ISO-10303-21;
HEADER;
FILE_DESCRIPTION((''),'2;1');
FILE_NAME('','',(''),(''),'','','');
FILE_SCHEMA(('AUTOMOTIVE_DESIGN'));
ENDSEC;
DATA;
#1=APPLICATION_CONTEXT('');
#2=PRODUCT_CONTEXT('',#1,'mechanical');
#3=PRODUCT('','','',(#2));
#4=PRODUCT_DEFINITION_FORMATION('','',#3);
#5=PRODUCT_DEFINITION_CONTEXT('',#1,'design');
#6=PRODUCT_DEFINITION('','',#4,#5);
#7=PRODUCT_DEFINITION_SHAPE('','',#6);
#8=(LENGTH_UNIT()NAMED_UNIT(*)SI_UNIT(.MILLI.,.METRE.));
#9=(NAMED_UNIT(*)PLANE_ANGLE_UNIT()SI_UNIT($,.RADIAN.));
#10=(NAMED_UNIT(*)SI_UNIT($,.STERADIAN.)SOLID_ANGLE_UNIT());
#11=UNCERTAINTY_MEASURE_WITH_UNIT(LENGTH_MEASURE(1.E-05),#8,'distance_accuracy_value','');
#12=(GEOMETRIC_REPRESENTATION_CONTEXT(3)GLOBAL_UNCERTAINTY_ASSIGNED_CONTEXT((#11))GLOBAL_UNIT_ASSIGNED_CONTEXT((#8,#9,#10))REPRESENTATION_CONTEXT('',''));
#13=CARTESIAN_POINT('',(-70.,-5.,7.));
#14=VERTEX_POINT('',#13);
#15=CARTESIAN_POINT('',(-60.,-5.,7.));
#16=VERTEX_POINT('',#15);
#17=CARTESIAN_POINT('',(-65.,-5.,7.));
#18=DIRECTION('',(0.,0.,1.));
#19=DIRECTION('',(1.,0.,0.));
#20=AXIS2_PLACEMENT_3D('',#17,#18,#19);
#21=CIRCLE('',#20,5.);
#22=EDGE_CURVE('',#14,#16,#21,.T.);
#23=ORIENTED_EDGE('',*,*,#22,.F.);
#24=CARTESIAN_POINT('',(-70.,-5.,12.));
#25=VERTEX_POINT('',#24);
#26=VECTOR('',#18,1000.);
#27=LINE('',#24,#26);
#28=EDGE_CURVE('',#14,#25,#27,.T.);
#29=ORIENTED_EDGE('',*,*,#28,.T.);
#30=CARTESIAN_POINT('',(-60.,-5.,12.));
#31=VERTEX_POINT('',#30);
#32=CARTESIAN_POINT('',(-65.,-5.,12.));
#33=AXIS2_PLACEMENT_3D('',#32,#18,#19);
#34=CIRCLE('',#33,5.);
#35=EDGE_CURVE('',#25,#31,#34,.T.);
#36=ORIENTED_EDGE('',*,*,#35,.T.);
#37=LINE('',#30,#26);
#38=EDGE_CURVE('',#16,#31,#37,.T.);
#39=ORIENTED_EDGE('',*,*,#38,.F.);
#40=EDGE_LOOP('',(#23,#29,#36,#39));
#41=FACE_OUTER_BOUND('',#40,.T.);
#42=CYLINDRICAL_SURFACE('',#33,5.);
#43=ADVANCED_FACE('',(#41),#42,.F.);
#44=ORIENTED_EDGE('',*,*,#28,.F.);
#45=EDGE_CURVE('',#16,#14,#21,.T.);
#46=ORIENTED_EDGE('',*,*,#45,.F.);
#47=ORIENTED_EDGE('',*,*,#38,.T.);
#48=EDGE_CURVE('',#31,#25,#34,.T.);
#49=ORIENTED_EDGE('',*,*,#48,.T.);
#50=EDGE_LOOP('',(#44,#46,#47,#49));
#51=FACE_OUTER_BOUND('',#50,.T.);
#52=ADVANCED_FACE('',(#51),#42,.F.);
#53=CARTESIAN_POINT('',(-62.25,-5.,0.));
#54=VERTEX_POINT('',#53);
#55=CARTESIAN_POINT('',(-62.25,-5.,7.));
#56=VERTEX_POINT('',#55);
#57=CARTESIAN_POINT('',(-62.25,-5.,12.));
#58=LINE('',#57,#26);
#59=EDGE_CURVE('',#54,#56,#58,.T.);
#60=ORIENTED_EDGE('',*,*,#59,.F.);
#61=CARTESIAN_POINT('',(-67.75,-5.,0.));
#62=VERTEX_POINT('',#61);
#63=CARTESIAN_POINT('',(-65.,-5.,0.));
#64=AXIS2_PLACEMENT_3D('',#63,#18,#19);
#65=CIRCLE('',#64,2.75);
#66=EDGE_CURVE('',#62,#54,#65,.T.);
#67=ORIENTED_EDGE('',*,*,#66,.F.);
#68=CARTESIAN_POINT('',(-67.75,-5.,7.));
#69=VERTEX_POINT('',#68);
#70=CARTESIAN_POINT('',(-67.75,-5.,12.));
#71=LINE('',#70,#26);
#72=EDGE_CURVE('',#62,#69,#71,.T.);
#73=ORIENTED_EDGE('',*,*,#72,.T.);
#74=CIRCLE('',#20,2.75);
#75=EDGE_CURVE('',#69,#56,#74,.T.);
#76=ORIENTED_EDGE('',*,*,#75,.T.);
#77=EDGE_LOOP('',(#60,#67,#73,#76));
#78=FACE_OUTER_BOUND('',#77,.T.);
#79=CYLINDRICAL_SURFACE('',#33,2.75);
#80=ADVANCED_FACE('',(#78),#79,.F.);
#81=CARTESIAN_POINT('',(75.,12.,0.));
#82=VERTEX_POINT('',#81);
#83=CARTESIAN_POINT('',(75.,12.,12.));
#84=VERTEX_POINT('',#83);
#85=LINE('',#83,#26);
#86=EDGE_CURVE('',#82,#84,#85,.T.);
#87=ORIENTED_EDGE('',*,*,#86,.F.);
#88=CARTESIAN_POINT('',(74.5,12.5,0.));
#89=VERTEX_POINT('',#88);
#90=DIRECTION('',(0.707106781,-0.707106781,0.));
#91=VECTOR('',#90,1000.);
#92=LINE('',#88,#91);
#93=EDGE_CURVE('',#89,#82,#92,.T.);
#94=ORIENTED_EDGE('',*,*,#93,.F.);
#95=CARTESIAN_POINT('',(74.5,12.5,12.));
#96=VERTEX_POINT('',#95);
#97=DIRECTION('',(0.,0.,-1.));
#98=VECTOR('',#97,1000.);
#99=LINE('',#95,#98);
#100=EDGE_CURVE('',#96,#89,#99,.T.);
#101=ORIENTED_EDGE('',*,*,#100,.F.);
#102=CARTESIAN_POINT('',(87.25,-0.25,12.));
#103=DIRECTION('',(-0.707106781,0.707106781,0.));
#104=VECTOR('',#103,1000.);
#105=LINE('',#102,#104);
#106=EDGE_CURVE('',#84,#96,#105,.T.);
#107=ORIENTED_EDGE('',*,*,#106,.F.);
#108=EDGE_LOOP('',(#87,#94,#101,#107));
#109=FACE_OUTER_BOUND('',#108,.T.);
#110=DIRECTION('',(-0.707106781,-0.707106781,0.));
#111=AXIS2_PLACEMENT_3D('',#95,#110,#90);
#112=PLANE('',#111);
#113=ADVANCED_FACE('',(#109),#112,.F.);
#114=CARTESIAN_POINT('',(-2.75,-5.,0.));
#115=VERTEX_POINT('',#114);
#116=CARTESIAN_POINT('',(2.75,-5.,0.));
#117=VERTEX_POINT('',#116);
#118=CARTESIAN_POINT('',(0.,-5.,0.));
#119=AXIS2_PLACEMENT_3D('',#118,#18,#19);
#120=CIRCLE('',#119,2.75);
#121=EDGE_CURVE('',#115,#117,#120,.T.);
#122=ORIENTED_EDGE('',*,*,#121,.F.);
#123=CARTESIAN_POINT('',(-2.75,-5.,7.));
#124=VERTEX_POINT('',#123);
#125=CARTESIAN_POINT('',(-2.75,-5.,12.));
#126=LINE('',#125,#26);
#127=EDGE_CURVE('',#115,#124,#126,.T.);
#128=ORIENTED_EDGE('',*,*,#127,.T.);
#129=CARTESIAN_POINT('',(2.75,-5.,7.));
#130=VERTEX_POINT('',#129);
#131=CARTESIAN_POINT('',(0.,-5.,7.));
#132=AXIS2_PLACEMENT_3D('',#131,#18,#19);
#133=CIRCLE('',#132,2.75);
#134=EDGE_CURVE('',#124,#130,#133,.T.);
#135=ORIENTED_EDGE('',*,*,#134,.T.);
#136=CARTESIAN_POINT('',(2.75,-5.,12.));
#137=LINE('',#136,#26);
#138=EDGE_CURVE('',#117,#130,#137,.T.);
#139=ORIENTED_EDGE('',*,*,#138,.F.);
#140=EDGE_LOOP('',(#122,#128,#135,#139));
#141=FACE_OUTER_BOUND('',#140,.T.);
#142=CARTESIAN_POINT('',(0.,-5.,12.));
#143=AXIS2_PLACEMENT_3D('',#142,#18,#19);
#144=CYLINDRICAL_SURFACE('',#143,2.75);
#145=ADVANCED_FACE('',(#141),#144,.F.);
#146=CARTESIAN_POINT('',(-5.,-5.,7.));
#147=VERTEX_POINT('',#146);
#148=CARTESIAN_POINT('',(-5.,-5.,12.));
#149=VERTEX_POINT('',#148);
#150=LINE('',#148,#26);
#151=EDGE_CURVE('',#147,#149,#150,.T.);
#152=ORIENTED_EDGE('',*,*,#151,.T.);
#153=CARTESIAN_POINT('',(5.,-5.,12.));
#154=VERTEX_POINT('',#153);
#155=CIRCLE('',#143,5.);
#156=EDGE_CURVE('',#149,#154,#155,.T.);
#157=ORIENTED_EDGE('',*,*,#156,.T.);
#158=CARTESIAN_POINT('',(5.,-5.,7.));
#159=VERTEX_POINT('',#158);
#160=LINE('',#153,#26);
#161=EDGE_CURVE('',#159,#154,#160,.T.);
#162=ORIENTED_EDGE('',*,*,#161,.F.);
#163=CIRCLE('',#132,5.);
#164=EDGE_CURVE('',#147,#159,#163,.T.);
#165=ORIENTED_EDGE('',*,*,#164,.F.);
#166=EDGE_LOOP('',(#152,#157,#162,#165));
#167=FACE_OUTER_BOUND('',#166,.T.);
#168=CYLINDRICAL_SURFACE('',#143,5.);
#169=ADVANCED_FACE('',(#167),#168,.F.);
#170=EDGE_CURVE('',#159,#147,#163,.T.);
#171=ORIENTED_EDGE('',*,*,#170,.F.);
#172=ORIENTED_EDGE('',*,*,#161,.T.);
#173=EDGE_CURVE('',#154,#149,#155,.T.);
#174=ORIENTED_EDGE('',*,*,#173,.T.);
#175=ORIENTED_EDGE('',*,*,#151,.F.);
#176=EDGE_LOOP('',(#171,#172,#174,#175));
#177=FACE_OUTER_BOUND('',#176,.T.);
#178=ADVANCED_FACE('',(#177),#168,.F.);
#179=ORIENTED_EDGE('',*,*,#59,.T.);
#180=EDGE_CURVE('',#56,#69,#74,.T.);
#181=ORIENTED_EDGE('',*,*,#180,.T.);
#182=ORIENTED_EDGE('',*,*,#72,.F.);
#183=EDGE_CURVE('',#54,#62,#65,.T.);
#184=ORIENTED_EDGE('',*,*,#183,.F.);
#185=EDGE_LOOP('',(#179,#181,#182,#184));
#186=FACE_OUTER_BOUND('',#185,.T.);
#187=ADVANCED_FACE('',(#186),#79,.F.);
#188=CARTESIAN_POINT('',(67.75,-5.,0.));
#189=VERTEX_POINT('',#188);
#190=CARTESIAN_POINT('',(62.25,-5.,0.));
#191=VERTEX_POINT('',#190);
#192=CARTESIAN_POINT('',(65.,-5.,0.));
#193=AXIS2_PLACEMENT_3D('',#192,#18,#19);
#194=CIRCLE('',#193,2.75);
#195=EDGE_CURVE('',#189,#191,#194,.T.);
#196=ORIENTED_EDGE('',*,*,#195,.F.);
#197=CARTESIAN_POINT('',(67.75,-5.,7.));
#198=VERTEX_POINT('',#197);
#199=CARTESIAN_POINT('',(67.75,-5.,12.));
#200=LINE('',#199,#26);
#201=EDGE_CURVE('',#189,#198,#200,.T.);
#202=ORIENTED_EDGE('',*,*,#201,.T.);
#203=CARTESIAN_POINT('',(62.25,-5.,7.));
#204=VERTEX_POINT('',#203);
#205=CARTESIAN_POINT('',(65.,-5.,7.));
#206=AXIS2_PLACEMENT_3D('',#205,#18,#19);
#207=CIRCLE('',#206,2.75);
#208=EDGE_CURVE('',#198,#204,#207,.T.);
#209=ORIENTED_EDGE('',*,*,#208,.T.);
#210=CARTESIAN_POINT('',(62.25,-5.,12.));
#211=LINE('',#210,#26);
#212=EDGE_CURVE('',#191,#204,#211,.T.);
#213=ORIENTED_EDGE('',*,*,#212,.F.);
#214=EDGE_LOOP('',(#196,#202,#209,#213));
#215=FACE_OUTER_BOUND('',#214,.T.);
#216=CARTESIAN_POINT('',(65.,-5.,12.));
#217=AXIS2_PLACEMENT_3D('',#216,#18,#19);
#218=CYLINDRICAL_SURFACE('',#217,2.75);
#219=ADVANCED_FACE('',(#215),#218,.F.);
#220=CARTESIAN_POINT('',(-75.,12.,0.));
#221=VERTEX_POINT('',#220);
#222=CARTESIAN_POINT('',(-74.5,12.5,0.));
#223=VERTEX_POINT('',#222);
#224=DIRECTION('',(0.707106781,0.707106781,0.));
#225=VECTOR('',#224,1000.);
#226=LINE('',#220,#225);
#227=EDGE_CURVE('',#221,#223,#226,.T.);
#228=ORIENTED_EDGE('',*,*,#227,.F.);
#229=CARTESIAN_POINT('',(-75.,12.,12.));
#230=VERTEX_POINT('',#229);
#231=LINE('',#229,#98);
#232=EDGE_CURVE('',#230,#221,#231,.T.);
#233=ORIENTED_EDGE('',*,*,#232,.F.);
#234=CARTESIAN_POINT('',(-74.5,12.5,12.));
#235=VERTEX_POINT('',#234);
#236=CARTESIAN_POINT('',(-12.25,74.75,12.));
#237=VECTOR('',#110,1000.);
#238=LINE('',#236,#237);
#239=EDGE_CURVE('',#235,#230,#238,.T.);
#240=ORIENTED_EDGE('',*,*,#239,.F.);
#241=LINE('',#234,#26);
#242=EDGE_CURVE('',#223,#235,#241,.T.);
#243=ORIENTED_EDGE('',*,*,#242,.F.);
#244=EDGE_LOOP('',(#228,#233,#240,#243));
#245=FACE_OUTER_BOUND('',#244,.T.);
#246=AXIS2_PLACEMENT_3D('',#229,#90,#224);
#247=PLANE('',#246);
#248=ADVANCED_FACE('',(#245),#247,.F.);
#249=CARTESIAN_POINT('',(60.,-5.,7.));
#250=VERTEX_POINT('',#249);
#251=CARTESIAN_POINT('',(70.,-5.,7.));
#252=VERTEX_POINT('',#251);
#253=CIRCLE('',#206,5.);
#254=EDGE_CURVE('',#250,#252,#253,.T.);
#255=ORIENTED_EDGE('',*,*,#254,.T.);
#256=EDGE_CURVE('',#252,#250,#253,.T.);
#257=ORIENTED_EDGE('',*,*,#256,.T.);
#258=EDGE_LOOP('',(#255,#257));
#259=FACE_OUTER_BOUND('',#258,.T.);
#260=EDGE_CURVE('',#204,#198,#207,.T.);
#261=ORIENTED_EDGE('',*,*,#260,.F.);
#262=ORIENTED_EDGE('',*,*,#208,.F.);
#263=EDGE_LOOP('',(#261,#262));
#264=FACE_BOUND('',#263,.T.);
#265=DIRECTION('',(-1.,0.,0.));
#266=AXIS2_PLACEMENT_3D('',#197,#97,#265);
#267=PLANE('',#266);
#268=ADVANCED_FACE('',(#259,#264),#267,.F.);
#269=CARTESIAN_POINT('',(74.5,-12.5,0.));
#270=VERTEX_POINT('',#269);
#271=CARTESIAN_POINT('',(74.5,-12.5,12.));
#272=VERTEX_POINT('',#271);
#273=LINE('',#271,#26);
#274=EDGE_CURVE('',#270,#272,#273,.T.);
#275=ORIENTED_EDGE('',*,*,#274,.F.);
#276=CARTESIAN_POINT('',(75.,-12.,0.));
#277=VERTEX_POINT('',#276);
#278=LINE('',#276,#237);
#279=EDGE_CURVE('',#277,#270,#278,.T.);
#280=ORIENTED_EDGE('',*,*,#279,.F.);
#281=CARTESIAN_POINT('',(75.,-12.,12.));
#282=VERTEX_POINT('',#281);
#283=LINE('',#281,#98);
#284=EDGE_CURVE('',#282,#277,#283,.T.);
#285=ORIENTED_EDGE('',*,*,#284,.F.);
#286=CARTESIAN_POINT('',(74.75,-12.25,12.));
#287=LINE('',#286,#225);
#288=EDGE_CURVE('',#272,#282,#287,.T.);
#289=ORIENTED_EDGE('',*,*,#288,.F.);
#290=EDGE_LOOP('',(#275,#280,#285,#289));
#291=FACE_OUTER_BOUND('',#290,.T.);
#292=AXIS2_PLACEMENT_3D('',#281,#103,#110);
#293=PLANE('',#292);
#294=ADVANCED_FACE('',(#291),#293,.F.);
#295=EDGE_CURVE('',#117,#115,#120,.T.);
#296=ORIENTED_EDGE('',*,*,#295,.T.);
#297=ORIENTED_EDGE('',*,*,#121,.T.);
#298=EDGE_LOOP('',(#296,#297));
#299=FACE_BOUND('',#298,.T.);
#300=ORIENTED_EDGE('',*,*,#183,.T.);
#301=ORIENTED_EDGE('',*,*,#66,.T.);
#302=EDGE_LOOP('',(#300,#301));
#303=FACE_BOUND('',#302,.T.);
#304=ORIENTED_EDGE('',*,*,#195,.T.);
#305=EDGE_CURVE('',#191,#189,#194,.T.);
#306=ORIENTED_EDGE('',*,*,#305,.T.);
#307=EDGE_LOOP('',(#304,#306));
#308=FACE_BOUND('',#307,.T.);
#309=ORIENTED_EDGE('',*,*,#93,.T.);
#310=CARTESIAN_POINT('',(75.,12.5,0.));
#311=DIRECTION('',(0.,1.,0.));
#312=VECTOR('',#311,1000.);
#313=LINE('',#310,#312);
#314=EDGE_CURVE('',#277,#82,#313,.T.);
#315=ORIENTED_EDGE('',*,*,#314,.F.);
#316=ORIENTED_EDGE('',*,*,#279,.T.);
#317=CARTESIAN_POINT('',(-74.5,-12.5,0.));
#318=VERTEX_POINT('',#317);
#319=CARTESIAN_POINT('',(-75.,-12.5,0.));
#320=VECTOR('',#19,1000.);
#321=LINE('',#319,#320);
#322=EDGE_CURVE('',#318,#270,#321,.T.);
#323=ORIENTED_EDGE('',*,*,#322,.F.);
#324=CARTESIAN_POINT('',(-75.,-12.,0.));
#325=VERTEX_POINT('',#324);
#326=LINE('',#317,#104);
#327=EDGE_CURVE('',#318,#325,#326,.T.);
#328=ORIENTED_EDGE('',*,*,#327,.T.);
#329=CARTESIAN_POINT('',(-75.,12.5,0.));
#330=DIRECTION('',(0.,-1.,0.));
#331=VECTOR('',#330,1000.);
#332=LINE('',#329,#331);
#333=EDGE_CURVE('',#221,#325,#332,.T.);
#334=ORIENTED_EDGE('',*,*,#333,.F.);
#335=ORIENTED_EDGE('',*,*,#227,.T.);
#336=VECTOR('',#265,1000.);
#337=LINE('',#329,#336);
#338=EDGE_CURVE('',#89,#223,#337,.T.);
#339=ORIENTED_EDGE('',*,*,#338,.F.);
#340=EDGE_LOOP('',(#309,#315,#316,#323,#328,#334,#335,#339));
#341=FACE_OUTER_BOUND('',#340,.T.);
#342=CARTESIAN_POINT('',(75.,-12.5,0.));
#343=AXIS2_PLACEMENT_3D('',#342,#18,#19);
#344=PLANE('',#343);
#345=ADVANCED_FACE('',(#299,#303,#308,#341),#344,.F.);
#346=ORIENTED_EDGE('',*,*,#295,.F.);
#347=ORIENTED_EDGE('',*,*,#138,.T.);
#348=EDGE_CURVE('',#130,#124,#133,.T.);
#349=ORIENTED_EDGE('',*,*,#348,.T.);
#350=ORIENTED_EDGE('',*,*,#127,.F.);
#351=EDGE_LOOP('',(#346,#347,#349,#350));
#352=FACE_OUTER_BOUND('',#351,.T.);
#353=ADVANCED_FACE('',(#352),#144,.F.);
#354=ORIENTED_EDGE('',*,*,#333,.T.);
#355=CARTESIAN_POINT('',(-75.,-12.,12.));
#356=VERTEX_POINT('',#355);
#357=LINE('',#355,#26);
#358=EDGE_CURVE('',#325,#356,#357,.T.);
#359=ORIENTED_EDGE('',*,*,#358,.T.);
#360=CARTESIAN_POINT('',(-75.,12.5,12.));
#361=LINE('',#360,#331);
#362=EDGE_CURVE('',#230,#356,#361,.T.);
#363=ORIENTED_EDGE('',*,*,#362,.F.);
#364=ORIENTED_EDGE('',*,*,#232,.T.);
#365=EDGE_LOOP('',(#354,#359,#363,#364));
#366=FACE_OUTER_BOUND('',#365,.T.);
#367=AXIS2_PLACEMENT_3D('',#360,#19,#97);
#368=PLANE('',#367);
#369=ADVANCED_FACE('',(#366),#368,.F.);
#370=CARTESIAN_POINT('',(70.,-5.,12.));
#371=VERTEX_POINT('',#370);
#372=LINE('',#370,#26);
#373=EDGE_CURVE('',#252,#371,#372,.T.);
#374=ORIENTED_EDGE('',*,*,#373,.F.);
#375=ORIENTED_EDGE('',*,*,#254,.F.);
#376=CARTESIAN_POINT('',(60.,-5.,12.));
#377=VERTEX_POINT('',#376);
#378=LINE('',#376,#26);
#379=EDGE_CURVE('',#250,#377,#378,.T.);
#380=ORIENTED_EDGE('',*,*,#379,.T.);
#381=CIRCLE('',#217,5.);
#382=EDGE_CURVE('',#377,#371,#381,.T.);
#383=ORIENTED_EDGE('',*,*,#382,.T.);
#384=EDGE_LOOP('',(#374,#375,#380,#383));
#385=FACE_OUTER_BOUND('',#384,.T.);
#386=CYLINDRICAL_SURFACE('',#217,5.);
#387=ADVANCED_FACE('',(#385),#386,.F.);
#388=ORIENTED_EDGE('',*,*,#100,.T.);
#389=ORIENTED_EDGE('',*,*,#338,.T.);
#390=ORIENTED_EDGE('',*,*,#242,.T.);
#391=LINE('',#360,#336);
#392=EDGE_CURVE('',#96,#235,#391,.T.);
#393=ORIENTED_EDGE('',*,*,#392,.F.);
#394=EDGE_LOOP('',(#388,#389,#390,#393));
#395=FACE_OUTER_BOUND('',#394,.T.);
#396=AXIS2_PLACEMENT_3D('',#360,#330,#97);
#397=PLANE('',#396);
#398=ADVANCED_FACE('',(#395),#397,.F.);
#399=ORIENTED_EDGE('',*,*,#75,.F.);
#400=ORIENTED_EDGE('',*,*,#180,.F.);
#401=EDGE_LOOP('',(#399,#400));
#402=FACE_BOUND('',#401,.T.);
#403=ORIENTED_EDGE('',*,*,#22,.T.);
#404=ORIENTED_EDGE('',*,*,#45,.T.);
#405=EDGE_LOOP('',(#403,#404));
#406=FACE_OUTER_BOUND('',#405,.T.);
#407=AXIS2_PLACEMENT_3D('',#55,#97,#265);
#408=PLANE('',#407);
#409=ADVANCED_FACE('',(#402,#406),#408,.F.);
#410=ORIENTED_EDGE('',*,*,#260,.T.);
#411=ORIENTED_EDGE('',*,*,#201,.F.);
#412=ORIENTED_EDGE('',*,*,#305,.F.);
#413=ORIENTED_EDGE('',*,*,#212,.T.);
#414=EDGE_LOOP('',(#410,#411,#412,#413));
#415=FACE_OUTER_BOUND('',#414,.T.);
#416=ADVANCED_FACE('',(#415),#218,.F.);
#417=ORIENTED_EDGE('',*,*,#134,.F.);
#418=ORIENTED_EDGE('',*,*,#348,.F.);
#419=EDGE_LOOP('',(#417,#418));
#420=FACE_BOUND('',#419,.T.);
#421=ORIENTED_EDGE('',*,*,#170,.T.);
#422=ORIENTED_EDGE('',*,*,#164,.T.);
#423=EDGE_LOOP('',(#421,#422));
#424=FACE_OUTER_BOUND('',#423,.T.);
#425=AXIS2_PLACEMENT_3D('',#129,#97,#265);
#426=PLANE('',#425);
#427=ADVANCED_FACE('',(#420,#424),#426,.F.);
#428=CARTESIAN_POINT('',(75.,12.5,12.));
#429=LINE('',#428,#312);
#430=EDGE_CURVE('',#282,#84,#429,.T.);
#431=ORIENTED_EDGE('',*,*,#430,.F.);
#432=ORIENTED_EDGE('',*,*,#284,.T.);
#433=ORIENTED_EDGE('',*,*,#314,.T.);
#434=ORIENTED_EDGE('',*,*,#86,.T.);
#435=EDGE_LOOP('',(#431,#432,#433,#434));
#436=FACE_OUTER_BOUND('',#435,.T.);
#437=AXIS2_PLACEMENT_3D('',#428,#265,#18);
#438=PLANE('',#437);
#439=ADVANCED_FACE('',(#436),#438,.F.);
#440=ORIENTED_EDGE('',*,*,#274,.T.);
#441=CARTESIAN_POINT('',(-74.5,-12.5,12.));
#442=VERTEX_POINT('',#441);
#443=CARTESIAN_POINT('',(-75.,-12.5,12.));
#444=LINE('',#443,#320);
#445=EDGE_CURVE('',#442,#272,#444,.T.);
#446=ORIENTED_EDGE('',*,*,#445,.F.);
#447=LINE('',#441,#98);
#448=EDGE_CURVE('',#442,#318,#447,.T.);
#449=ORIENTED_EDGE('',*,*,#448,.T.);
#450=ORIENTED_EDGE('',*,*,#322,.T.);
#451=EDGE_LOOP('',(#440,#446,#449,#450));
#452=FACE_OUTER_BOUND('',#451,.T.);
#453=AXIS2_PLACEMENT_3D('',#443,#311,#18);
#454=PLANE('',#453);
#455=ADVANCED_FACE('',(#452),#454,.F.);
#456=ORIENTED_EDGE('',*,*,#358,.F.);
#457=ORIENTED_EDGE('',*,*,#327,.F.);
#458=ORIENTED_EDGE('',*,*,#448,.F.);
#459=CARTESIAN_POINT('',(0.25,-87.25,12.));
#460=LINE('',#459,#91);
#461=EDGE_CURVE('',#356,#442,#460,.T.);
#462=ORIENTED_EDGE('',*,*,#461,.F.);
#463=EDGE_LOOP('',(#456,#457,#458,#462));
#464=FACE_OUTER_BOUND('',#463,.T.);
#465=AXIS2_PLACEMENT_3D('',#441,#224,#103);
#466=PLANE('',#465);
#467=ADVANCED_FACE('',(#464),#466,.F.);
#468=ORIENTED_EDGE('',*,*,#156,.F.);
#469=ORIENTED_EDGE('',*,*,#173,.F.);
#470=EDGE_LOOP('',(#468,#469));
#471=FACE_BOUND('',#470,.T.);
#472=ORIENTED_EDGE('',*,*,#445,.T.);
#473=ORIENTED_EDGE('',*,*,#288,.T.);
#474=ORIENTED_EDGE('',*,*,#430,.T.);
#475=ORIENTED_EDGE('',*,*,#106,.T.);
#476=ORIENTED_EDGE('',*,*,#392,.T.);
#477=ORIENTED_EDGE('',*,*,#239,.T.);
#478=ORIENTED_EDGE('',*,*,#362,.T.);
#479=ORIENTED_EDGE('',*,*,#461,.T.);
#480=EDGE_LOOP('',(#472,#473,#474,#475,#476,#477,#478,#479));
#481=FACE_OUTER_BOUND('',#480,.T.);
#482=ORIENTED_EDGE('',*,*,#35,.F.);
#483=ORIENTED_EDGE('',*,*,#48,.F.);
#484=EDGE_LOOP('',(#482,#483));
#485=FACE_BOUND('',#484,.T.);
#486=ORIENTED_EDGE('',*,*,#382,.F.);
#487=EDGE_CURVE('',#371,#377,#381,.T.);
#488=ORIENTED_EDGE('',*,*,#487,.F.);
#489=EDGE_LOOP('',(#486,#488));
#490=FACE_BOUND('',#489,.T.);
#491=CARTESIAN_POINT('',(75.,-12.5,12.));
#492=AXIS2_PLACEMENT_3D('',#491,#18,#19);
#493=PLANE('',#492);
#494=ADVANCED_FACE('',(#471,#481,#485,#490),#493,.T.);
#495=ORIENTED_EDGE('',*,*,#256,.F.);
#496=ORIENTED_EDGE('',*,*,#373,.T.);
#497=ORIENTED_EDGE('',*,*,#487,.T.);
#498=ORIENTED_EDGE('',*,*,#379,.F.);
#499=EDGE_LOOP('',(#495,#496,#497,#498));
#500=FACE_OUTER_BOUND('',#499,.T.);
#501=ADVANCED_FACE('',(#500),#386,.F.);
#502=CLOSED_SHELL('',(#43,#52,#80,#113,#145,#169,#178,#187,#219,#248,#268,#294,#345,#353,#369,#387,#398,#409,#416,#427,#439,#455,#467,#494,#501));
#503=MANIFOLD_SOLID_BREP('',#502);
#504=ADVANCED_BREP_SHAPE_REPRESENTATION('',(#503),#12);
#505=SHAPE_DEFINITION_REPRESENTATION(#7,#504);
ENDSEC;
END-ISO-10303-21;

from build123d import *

# Parameters (mm, degrees)
SKETCH1_W                                           = 150
SKETCH1_H                                           = 25
BOSS_EXTRUDE1_DEPTH                                 = 12
CBORE_FOR_M5_HEX_SOCKET_HEAD_CAP_SCREW1_D           = 5.5
CBORE_FOR_M5_HEX_SOCKET_HEAD_CAP_SCREW1_CBORE_D     = 10
CBORE_FOR_M5_HEX_SOCKET_HEAD_CAP_SCREW1_CBORE_DEPTH = 5
CHAMFER1_SIZE                                       = 0.5


with BuildPart() as part:
    # Sketch1 → Boss-Extrude1 (new body)
    with BuildSketch(Plane.XY):
        Rectangle(SKETCH1_W, SKETCH1_H)
    extrude(amount=BOSS_EXTRUDE1_DEPTH)

    # CBORE for M5 Hex Socket Head Cap Screw1 (through all)
    with Locations(Plane.XY.offset(12)):
        with Locations((0, -5), (-65, -5), (65, -5)):
            CounterBoreHole(CBORE_FOR_M5_HEX_SOCKET_HEAD_CAP_SCREW1_D / 2, CBORE_FOR_M5_HEX_SOCKET_HEAD_CAP_SCREW1_CBORE_D / 2, CBORE_FOR_M5_HEX_SOCKET_HEAD_CAP_SCREW1_CBORE_DEPTH)

    # Chamfer1
    chamfer1_edges = [part.edges().sort_by_distance(p)[0] for p in [
        (75, -12.5, 6),
        (-75, -12.5, 6),
        (-75, 12.5, 6),
        (75, 12.5, 6),
    ]]
    chamfer(chamfer1_edges, length=CHAMFER1_SIZE)


solid = part.part
